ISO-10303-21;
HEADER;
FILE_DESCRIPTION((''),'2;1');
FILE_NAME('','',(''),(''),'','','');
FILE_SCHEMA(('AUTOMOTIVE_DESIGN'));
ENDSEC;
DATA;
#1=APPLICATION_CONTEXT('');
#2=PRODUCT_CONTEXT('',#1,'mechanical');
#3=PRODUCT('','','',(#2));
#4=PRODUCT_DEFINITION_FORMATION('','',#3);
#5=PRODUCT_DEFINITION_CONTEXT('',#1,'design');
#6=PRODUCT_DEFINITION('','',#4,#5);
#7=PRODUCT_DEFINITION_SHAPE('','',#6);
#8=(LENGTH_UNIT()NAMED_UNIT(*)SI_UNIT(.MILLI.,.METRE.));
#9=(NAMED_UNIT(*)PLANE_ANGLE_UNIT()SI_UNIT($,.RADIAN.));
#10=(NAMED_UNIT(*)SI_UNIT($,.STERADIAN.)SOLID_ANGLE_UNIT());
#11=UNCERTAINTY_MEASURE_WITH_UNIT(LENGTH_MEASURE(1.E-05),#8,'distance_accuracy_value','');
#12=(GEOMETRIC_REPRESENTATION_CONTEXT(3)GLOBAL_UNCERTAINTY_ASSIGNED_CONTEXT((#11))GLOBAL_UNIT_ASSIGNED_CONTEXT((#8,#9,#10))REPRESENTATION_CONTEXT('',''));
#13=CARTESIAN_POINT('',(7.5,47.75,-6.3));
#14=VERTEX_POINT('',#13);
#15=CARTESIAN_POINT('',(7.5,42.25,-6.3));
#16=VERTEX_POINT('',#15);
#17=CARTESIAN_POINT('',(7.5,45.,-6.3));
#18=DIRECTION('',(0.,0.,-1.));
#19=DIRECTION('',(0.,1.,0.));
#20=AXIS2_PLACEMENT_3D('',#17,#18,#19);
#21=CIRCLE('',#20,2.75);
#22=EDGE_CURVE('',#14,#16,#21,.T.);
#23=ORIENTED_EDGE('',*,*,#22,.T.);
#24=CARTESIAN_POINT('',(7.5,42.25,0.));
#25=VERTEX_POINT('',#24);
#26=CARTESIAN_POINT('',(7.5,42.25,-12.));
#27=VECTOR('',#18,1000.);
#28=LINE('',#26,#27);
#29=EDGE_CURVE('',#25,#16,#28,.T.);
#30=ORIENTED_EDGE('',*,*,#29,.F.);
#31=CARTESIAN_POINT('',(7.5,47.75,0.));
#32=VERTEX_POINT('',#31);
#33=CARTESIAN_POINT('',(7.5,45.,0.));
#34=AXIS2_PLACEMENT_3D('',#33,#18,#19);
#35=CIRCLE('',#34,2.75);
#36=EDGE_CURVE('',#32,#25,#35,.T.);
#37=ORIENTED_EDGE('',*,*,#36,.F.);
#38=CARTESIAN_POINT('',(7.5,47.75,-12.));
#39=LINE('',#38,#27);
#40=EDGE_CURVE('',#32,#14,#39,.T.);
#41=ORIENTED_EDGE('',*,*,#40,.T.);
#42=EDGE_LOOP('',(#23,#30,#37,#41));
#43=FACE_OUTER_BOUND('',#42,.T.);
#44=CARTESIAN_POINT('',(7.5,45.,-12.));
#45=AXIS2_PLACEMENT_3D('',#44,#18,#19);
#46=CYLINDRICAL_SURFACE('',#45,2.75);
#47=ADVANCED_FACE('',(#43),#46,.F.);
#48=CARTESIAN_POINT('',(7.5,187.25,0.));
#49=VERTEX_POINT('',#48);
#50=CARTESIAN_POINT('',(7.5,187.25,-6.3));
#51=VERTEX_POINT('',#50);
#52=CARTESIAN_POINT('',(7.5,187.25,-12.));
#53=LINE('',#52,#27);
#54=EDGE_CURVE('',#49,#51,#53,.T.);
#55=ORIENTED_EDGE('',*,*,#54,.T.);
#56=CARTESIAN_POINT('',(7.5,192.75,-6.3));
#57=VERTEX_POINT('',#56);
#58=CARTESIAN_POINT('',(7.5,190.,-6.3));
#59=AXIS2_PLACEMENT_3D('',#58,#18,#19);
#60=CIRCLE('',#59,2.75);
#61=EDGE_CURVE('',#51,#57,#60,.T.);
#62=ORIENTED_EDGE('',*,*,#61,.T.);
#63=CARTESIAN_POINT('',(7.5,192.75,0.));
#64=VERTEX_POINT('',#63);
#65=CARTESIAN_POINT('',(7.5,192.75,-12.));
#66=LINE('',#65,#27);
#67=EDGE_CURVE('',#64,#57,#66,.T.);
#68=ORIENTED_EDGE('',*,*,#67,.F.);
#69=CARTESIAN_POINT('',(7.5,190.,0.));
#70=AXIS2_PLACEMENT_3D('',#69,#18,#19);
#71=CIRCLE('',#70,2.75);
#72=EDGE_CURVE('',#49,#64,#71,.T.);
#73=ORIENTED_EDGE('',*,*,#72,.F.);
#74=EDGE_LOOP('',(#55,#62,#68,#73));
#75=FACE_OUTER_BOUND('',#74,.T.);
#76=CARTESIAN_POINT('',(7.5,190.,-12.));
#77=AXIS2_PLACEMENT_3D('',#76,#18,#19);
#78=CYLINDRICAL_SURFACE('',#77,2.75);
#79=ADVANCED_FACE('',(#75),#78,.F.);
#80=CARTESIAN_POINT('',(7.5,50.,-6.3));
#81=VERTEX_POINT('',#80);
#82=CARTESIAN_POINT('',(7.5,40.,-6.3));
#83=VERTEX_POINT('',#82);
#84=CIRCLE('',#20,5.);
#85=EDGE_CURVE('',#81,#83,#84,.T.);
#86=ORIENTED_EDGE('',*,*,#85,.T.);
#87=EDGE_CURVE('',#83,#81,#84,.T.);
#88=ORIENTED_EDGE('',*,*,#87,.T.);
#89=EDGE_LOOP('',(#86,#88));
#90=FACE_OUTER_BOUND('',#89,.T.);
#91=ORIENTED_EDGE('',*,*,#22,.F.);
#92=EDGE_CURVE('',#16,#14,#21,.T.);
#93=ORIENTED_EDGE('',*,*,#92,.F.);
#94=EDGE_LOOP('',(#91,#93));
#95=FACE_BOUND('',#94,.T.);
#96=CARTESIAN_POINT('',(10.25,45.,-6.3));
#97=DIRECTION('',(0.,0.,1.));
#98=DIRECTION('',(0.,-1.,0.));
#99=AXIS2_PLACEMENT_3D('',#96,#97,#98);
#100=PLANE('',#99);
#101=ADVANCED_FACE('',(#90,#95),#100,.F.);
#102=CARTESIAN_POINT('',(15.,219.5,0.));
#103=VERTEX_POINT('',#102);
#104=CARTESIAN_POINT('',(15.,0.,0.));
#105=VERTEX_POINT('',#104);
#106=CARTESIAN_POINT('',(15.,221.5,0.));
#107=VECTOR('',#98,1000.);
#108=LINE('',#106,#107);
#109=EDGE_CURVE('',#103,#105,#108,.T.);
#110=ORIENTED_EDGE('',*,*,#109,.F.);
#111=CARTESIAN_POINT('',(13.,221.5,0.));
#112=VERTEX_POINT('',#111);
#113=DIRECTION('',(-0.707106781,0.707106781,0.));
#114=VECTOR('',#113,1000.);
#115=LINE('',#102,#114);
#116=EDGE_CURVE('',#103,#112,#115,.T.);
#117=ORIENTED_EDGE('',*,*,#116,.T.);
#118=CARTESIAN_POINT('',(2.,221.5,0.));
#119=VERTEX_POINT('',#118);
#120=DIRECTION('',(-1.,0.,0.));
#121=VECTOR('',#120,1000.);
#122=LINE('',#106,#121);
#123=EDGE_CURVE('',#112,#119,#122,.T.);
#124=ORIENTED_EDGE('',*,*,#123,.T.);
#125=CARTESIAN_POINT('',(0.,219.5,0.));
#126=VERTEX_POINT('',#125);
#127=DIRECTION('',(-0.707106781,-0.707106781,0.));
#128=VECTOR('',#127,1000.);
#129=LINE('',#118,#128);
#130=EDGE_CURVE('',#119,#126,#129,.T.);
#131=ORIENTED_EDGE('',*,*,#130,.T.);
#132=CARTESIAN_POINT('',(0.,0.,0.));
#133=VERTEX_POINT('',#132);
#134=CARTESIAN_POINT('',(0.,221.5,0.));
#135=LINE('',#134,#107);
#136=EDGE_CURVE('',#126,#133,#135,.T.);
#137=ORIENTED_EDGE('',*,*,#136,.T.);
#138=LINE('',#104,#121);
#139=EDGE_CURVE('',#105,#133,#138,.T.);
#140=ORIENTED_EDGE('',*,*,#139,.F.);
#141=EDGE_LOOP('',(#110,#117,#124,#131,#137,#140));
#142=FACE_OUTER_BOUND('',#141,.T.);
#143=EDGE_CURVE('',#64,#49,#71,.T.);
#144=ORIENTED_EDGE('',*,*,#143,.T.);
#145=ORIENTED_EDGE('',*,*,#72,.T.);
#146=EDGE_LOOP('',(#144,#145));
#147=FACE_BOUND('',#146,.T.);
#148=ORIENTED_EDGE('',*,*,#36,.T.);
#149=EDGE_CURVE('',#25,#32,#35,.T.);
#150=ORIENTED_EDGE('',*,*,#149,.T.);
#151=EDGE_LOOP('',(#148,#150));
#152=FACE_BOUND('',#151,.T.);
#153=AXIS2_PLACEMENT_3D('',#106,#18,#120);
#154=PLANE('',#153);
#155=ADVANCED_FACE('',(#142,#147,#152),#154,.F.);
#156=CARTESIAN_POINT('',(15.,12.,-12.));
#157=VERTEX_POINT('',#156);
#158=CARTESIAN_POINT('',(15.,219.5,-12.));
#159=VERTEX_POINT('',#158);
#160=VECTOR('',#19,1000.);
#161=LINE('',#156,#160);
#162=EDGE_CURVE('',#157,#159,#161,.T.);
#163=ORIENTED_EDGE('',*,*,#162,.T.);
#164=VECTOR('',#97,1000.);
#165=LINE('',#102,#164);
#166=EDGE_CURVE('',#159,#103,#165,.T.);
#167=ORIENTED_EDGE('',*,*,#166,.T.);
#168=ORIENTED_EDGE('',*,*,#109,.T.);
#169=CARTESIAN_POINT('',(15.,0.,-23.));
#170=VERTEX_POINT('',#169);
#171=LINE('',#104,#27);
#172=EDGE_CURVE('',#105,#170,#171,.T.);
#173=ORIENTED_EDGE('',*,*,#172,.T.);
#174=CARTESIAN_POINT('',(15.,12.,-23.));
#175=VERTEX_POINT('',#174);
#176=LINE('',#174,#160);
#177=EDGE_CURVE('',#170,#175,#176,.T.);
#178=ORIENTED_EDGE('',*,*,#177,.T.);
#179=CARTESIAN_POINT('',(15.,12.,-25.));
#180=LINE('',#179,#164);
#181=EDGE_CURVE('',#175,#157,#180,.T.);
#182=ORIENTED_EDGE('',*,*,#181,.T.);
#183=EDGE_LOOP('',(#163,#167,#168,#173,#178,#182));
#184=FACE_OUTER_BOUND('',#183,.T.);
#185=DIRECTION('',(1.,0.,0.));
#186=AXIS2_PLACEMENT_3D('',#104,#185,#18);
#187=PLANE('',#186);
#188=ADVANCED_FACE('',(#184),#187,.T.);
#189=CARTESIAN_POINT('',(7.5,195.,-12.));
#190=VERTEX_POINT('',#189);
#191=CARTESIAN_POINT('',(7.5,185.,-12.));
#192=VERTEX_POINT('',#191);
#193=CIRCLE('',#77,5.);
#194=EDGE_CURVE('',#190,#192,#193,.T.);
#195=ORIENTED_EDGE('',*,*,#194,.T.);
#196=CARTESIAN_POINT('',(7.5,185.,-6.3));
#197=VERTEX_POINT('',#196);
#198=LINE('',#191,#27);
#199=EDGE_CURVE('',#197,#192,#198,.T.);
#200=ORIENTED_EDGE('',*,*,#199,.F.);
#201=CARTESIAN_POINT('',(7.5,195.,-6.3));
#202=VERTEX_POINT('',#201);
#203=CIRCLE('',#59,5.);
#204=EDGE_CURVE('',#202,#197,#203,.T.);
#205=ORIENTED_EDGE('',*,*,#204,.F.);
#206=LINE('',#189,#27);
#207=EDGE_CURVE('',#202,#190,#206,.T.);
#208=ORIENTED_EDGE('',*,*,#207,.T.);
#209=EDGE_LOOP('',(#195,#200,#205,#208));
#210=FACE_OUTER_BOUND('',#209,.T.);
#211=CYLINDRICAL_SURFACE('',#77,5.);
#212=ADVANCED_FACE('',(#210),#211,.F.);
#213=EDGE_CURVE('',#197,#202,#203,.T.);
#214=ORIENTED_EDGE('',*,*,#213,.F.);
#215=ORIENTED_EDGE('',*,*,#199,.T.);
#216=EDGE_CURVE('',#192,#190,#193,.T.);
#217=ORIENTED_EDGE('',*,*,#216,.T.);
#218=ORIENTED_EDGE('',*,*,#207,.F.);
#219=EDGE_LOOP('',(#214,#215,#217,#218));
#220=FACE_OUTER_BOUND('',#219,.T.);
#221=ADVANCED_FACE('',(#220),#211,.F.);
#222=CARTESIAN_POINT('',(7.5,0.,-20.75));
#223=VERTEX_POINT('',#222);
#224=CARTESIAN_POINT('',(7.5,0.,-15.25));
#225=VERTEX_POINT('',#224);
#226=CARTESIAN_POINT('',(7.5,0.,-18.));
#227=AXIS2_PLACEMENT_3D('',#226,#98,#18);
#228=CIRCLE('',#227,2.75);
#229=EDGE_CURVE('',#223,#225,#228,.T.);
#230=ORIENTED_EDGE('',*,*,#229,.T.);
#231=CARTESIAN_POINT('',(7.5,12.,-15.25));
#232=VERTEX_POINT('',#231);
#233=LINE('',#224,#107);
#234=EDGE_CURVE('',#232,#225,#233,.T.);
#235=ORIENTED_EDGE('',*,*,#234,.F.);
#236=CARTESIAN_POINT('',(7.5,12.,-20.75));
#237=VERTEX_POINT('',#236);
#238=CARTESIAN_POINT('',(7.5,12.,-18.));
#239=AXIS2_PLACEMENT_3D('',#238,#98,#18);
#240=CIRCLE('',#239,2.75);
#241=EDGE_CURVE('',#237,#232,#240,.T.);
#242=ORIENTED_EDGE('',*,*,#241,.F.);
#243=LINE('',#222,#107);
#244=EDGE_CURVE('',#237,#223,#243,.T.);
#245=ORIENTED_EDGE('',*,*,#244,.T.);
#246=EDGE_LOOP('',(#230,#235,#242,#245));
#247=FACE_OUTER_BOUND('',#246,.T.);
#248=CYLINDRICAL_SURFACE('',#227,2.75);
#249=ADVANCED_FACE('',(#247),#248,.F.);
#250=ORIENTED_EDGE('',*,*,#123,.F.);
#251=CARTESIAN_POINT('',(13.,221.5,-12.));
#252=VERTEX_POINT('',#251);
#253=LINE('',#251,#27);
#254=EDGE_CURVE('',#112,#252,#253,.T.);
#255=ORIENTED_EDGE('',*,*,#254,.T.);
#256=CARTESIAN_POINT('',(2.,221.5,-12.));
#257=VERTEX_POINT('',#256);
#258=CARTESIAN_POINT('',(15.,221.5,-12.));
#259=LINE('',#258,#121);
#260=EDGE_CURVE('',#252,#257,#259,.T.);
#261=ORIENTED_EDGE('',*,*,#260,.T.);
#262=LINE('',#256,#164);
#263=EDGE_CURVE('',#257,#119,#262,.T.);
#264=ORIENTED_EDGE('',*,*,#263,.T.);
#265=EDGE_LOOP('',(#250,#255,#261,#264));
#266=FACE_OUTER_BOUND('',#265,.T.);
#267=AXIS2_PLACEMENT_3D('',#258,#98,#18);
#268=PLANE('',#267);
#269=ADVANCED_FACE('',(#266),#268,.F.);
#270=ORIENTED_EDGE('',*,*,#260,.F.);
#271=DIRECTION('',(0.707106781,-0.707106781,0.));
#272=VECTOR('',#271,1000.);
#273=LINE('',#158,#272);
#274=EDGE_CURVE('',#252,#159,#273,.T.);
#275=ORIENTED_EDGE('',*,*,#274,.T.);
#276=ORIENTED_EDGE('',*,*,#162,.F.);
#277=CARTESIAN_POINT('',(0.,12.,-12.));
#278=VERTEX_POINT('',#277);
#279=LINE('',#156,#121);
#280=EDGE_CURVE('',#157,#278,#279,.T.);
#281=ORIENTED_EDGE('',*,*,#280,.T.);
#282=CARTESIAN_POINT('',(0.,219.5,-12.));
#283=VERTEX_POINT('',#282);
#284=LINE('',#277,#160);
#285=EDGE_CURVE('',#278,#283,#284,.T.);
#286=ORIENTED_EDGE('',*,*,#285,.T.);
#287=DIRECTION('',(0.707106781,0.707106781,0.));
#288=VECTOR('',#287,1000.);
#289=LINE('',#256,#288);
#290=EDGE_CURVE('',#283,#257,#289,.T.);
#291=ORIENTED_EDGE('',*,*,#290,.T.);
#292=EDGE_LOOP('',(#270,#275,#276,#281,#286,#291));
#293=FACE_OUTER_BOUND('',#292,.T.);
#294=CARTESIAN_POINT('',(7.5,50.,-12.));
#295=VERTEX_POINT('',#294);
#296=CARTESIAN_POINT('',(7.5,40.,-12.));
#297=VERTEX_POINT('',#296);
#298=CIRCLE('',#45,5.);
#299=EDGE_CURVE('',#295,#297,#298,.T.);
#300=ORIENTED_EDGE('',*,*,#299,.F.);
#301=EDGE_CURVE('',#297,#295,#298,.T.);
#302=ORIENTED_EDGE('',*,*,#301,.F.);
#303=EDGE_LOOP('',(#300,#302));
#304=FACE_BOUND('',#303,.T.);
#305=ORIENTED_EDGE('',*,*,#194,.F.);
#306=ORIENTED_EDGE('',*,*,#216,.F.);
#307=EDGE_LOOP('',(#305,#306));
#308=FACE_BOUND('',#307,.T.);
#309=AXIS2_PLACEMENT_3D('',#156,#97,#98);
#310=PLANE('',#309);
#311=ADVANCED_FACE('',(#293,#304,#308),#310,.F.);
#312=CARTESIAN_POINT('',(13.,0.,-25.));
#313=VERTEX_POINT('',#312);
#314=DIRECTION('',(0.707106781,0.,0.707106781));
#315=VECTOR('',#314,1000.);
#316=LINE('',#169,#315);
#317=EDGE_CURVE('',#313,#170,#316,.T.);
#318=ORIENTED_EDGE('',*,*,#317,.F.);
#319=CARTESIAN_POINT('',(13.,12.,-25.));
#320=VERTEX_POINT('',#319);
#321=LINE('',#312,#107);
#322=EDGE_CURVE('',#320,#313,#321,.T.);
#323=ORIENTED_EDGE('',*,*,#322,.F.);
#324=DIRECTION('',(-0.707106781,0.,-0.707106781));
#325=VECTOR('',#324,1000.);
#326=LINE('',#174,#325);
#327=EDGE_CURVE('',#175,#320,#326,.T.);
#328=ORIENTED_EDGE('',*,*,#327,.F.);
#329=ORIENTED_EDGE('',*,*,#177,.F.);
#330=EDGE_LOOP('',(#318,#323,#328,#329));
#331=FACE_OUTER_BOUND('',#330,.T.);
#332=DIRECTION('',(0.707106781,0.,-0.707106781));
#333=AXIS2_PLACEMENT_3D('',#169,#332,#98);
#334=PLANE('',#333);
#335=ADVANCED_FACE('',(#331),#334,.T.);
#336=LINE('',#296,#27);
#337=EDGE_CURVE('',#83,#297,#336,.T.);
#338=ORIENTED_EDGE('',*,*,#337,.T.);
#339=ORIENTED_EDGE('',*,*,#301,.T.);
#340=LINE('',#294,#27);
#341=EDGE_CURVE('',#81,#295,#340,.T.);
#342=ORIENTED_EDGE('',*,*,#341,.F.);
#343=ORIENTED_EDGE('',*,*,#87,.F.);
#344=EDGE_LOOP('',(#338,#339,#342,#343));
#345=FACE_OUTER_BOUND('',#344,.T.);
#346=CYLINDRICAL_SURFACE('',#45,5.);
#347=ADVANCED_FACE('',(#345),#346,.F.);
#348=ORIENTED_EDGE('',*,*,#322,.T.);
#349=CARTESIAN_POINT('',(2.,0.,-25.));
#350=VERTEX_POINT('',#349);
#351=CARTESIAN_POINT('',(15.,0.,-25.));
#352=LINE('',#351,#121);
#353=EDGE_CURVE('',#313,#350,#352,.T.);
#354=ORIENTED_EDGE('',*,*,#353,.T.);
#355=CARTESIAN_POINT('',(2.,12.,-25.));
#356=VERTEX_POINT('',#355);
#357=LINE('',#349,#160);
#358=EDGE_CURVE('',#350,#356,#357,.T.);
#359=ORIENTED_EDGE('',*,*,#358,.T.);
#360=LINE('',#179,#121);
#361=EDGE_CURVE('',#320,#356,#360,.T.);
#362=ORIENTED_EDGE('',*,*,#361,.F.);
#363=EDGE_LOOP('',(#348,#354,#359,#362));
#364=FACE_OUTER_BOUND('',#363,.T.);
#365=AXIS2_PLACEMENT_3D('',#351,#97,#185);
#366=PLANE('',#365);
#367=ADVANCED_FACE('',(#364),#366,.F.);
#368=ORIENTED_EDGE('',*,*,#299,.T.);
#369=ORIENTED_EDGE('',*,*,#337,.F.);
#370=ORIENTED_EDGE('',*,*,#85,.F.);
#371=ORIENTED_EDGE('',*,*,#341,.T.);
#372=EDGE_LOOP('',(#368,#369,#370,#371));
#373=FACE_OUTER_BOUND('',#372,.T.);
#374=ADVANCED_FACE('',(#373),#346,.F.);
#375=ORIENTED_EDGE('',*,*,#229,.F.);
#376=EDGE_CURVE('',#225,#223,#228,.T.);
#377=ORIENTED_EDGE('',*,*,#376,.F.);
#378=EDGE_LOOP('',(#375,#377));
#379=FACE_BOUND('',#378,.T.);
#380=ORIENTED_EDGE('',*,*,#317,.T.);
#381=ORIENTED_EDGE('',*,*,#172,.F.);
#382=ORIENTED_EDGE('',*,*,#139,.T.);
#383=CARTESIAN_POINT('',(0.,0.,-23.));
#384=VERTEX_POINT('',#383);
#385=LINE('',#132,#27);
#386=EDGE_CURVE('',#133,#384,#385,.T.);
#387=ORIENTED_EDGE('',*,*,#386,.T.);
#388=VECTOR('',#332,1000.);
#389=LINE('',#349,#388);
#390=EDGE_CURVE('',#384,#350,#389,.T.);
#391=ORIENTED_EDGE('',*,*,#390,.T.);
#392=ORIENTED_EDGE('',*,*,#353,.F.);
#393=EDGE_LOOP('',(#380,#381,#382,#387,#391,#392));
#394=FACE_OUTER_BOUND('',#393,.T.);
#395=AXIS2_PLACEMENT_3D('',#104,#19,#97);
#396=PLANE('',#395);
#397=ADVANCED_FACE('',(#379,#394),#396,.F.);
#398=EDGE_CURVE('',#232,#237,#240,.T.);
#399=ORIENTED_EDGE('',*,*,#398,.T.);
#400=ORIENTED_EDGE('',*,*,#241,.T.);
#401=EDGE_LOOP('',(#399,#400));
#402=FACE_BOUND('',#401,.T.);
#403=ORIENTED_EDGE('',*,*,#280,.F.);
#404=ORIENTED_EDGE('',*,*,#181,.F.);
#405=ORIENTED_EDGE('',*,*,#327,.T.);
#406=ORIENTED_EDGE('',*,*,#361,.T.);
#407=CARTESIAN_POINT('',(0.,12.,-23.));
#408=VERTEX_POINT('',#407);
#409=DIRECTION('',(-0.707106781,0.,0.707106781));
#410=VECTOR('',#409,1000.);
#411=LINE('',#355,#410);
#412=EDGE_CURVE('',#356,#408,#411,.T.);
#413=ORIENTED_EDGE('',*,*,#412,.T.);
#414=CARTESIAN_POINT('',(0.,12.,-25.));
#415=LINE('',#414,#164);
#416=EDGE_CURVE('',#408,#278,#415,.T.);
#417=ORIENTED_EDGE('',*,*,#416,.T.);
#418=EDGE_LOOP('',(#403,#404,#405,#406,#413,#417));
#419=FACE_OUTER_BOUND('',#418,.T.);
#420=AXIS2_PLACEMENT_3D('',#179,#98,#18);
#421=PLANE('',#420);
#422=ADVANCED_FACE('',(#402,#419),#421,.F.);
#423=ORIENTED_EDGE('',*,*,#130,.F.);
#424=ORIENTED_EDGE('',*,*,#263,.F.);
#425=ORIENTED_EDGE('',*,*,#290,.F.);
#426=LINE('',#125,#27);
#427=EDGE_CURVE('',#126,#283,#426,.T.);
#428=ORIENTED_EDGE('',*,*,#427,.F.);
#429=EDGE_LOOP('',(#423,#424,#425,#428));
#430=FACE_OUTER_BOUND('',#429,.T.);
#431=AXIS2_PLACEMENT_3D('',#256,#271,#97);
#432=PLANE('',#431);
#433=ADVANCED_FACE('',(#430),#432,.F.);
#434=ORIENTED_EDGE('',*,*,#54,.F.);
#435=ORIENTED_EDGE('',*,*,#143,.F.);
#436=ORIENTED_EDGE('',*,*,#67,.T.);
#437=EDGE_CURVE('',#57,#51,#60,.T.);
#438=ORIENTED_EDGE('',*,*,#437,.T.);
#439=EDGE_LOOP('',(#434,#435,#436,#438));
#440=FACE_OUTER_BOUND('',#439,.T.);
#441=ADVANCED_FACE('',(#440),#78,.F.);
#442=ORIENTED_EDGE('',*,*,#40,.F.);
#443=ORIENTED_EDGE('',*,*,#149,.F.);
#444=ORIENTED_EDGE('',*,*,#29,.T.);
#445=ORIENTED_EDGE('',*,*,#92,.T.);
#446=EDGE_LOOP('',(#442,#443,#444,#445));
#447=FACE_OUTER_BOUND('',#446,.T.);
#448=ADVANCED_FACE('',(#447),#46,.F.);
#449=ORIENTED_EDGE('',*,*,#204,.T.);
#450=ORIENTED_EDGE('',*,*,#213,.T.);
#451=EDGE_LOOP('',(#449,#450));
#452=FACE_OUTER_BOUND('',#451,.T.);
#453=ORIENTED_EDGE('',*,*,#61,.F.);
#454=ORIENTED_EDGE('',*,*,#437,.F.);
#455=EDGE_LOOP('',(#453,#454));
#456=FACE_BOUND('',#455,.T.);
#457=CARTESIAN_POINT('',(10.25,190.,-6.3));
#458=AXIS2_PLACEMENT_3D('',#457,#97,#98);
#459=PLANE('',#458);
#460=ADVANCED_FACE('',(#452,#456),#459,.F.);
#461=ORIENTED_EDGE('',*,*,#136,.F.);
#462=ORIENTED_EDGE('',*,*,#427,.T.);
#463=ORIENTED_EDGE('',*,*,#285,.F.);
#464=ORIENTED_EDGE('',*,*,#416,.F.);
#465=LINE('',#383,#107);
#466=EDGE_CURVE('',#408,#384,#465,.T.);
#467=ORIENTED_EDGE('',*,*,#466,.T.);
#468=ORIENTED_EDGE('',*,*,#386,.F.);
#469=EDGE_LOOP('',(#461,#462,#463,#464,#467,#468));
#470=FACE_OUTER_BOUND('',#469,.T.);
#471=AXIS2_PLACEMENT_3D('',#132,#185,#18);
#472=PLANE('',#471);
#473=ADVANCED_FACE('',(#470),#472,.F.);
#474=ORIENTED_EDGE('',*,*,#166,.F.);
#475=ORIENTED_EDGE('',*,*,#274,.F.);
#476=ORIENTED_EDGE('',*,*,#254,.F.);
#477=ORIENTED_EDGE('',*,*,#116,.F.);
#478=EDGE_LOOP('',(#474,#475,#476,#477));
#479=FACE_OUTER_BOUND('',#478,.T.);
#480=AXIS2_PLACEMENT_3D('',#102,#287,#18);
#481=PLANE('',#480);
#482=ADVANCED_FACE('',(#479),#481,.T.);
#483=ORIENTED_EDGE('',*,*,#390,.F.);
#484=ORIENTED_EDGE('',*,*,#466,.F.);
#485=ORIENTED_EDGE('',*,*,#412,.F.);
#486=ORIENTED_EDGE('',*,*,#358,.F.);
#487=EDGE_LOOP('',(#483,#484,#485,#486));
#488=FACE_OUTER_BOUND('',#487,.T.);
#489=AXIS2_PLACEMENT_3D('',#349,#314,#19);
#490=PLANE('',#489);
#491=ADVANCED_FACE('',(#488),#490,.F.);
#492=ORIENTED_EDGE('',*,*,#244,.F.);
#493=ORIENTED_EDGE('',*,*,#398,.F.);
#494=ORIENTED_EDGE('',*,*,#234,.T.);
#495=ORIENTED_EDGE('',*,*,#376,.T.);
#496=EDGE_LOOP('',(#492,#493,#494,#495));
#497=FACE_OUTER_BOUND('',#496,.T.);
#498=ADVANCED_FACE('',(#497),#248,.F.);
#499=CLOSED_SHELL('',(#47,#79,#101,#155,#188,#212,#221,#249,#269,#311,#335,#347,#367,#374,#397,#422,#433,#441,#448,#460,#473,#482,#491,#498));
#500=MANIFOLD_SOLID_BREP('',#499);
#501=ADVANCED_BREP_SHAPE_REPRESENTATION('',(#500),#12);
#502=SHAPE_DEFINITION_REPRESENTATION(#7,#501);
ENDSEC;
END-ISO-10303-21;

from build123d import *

# Parameters (mm, degrees)
BOSS_EXTRUDE1_DEPTH                                  = 15
CBORE_FOR_M5_HEXAGON_SOCKET_HEAD_CAP_SCR_D           = 5.5
CBORE_FOR_M5_HEXAGON_SOCKET_HEAD_CAP_SCR_CBORE_D     = 10
CBORE_FOR_M5_HEXAGON_SOCKET_HEAD_CAP_SCR_CBORE_DEPTH = 5.7
M5_CLEARANCE_HOLE1_D                                 = 5.5
CHAMFER1_SIZE                                        = 2


with BuildPart() as part:
    # Sketch1 → Boss-Extrude1 (new body)
    with BuildSketch(Plane(origin=(0, 0, 0), x_dir=(0, 0, -1), z_dir=(1, 0, 0))):
        Polygon((0, 0), (25, 0), (25, 12), (12, 12), (12, 221.5), (0, 221.5), align=None)
    extrude(amount=BOSS_EXTRUDE1_DEPTH)

    # CBORE for M5 Hexagon socket head cap screws1 (through all)
    with Locations(Plane(origin=(0, 0, -12), x_dir=(-1, 0, 0), z_dir=(0, 0, -1))):
        with Locations((-7.5, 45), (-7.5, 190)):
            CounterBoreHole(CBORE_FOR_M5_HEXAGON_SOCKET_HEAD_CAP_SCR_D / 2, CBORE_FOR_M5_HEXAGON_SOCKET_HEAD_CAP_SCR_CBORE_D / 2, CBORE_FOR_M5_HEXAGON_SOCKET_HEAD_CAP_SCR_CBORE_DEPTH)

    # M5 Clearance Hole1 (through all)
    with Locations(Plane(origin=(0, 0, 0), x_dir=(-1, 0, 0), z_dir=(0, -1, 0))):
        with Locations((-7.5, 18)):
            Hole(M5_CLEARANCE_HOLE1_D / 2)

    # Chamfer1
    chamfer1_edges = [part.edges().sort_by_distance(p)[0] for p in [
        (15, 6, -25),
        (15, 221.5, -6),
        (0, 221.5, -6),
        (0, 6, -25),
    ]]
    chamfer(chamfer1_edges, length=CHAMFER1_SIZE)


solid = part.part
